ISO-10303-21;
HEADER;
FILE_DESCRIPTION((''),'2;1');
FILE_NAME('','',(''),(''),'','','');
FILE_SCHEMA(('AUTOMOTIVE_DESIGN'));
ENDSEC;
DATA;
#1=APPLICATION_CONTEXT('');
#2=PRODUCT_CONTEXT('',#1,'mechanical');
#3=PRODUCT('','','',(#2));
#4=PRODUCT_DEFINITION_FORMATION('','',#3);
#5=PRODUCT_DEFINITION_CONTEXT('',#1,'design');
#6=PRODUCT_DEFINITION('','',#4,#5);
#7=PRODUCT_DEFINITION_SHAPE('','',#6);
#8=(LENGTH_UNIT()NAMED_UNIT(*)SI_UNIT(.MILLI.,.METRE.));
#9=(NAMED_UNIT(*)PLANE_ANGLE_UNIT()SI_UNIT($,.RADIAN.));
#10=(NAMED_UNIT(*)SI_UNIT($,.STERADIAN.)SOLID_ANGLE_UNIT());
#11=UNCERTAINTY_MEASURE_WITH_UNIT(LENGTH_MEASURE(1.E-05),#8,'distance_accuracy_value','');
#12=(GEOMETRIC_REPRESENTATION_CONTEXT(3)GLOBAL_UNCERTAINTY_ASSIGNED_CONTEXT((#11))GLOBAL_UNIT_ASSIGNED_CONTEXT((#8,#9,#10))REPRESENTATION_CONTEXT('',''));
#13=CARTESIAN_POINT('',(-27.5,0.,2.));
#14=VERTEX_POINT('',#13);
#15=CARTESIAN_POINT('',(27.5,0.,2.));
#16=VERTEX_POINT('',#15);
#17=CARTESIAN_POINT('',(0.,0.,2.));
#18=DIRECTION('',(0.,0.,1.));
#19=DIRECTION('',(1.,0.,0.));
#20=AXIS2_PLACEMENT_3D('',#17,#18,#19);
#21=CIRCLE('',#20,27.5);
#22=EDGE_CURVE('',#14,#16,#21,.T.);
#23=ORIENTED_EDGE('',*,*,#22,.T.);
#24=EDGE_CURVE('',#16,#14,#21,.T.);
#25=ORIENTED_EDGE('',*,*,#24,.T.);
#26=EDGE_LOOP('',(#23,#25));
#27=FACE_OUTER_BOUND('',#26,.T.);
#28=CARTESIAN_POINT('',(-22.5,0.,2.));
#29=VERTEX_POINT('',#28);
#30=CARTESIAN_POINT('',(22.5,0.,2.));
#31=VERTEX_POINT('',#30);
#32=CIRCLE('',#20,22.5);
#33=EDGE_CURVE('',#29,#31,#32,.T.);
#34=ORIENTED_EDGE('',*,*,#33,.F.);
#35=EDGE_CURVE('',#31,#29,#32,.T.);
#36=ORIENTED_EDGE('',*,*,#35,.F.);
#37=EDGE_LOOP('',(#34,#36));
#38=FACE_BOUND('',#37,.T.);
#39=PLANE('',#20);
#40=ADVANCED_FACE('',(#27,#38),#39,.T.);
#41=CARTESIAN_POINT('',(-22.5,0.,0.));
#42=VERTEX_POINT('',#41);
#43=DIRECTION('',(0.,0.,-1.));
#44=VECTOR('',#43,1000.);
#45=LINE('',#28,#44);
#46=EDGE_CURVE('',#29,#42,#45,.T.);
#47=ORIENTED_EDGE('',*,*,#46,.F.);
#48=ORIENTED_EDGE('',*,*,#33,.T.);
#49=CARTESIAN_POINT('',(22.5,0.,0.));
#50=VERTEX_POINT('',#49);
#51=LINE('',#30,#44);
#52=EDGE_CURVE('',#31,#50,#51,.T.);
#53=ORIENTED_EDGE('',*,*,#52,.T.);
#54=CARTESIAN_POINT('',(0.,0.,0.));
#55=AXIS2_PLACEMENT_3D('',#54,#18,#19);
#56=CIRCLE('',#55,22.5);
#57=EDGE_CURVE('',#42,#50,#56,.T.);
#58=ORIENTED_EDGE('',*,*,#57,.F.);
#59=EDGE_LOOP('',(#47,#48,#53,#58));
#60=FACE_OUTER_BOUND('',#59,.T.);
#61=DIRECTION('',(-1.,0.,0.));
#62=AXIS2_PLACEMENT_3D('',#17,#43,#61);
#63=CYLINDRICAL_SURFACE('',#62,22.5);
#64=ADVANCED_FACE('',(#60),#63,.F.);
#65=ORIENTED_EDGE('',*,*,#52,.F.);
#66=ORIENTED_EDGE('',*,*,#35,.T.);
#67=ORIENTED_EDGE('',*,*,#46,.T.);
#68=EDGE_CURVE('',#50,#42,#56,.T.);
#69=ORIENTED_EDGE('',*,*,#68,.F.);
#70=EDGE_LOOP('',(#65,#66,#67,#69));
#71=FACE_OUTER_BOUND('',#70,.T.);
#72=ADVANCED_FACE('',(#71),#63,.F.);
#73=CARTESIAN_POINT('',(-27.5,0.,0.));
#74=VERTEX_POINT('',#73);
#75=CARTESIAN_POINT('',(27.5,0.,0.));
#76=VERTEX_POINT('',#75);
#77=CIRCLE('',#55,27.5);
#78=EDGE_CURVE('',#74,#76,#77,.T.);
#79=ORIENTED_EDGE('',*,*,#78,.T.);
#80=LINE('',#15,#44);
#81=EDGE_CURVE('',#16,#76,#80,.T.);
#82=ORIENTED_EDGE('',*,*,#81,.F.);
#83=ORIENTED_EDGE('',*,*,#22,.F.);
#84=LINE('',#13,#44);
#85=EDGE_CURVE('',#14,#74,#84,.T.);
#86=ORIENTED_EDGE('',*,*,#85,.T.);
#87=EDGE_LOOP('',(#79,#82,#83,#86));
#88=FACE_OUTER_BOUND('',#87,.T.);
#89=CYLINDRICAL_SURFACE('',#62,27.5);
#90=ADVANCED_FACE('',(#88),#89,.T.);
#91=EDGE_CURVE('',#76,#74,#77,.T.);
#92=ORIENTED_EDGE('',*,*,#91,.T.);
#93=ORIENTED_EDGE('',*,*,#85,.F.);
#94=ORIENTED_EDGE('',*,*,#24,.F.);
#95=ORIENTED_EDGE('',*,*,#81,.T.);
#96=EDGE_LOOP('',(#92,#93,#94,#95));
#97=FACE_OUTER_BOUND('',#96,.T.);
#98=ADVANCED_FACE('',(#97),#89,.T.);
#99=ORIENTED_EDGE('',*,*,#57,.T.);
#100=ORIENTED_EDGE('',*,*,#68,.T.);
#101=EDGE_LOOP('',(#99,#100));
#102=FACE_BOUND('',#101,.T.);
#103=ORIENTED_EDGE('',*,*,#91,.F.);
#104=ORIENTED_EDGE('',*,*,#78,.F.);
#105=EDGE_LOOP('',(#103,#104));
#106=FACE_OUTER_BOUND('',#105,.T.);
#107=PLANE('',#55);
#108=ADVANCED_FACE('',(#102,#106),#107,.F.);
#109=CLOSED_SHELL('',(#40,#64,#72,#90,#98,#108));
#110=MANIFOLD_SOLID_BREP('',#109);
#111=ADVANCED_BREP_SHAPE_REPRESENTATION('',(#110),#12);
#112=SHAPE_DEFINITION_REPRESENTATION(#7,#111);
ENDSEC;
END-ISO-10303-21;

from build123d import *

# Parameters (mm, degrees)
SKETCH_1_R      = 27.5
SKETCH_1_R_2    = 22.5
EXTRUDE_1_DEPTH = 2


with BuildPart() as part:
    # 草图1 → 凸台-拉伸1 (new body)
    with BuildSketch(Plane.XY):
        Circle(SKETCH_1_R)
        Circle(SKETCH_1_R_2, mode=Mode.SUBTRACT)
    extrude(amount=EXTRUDE_1_DEPTH)


solid = part.part
